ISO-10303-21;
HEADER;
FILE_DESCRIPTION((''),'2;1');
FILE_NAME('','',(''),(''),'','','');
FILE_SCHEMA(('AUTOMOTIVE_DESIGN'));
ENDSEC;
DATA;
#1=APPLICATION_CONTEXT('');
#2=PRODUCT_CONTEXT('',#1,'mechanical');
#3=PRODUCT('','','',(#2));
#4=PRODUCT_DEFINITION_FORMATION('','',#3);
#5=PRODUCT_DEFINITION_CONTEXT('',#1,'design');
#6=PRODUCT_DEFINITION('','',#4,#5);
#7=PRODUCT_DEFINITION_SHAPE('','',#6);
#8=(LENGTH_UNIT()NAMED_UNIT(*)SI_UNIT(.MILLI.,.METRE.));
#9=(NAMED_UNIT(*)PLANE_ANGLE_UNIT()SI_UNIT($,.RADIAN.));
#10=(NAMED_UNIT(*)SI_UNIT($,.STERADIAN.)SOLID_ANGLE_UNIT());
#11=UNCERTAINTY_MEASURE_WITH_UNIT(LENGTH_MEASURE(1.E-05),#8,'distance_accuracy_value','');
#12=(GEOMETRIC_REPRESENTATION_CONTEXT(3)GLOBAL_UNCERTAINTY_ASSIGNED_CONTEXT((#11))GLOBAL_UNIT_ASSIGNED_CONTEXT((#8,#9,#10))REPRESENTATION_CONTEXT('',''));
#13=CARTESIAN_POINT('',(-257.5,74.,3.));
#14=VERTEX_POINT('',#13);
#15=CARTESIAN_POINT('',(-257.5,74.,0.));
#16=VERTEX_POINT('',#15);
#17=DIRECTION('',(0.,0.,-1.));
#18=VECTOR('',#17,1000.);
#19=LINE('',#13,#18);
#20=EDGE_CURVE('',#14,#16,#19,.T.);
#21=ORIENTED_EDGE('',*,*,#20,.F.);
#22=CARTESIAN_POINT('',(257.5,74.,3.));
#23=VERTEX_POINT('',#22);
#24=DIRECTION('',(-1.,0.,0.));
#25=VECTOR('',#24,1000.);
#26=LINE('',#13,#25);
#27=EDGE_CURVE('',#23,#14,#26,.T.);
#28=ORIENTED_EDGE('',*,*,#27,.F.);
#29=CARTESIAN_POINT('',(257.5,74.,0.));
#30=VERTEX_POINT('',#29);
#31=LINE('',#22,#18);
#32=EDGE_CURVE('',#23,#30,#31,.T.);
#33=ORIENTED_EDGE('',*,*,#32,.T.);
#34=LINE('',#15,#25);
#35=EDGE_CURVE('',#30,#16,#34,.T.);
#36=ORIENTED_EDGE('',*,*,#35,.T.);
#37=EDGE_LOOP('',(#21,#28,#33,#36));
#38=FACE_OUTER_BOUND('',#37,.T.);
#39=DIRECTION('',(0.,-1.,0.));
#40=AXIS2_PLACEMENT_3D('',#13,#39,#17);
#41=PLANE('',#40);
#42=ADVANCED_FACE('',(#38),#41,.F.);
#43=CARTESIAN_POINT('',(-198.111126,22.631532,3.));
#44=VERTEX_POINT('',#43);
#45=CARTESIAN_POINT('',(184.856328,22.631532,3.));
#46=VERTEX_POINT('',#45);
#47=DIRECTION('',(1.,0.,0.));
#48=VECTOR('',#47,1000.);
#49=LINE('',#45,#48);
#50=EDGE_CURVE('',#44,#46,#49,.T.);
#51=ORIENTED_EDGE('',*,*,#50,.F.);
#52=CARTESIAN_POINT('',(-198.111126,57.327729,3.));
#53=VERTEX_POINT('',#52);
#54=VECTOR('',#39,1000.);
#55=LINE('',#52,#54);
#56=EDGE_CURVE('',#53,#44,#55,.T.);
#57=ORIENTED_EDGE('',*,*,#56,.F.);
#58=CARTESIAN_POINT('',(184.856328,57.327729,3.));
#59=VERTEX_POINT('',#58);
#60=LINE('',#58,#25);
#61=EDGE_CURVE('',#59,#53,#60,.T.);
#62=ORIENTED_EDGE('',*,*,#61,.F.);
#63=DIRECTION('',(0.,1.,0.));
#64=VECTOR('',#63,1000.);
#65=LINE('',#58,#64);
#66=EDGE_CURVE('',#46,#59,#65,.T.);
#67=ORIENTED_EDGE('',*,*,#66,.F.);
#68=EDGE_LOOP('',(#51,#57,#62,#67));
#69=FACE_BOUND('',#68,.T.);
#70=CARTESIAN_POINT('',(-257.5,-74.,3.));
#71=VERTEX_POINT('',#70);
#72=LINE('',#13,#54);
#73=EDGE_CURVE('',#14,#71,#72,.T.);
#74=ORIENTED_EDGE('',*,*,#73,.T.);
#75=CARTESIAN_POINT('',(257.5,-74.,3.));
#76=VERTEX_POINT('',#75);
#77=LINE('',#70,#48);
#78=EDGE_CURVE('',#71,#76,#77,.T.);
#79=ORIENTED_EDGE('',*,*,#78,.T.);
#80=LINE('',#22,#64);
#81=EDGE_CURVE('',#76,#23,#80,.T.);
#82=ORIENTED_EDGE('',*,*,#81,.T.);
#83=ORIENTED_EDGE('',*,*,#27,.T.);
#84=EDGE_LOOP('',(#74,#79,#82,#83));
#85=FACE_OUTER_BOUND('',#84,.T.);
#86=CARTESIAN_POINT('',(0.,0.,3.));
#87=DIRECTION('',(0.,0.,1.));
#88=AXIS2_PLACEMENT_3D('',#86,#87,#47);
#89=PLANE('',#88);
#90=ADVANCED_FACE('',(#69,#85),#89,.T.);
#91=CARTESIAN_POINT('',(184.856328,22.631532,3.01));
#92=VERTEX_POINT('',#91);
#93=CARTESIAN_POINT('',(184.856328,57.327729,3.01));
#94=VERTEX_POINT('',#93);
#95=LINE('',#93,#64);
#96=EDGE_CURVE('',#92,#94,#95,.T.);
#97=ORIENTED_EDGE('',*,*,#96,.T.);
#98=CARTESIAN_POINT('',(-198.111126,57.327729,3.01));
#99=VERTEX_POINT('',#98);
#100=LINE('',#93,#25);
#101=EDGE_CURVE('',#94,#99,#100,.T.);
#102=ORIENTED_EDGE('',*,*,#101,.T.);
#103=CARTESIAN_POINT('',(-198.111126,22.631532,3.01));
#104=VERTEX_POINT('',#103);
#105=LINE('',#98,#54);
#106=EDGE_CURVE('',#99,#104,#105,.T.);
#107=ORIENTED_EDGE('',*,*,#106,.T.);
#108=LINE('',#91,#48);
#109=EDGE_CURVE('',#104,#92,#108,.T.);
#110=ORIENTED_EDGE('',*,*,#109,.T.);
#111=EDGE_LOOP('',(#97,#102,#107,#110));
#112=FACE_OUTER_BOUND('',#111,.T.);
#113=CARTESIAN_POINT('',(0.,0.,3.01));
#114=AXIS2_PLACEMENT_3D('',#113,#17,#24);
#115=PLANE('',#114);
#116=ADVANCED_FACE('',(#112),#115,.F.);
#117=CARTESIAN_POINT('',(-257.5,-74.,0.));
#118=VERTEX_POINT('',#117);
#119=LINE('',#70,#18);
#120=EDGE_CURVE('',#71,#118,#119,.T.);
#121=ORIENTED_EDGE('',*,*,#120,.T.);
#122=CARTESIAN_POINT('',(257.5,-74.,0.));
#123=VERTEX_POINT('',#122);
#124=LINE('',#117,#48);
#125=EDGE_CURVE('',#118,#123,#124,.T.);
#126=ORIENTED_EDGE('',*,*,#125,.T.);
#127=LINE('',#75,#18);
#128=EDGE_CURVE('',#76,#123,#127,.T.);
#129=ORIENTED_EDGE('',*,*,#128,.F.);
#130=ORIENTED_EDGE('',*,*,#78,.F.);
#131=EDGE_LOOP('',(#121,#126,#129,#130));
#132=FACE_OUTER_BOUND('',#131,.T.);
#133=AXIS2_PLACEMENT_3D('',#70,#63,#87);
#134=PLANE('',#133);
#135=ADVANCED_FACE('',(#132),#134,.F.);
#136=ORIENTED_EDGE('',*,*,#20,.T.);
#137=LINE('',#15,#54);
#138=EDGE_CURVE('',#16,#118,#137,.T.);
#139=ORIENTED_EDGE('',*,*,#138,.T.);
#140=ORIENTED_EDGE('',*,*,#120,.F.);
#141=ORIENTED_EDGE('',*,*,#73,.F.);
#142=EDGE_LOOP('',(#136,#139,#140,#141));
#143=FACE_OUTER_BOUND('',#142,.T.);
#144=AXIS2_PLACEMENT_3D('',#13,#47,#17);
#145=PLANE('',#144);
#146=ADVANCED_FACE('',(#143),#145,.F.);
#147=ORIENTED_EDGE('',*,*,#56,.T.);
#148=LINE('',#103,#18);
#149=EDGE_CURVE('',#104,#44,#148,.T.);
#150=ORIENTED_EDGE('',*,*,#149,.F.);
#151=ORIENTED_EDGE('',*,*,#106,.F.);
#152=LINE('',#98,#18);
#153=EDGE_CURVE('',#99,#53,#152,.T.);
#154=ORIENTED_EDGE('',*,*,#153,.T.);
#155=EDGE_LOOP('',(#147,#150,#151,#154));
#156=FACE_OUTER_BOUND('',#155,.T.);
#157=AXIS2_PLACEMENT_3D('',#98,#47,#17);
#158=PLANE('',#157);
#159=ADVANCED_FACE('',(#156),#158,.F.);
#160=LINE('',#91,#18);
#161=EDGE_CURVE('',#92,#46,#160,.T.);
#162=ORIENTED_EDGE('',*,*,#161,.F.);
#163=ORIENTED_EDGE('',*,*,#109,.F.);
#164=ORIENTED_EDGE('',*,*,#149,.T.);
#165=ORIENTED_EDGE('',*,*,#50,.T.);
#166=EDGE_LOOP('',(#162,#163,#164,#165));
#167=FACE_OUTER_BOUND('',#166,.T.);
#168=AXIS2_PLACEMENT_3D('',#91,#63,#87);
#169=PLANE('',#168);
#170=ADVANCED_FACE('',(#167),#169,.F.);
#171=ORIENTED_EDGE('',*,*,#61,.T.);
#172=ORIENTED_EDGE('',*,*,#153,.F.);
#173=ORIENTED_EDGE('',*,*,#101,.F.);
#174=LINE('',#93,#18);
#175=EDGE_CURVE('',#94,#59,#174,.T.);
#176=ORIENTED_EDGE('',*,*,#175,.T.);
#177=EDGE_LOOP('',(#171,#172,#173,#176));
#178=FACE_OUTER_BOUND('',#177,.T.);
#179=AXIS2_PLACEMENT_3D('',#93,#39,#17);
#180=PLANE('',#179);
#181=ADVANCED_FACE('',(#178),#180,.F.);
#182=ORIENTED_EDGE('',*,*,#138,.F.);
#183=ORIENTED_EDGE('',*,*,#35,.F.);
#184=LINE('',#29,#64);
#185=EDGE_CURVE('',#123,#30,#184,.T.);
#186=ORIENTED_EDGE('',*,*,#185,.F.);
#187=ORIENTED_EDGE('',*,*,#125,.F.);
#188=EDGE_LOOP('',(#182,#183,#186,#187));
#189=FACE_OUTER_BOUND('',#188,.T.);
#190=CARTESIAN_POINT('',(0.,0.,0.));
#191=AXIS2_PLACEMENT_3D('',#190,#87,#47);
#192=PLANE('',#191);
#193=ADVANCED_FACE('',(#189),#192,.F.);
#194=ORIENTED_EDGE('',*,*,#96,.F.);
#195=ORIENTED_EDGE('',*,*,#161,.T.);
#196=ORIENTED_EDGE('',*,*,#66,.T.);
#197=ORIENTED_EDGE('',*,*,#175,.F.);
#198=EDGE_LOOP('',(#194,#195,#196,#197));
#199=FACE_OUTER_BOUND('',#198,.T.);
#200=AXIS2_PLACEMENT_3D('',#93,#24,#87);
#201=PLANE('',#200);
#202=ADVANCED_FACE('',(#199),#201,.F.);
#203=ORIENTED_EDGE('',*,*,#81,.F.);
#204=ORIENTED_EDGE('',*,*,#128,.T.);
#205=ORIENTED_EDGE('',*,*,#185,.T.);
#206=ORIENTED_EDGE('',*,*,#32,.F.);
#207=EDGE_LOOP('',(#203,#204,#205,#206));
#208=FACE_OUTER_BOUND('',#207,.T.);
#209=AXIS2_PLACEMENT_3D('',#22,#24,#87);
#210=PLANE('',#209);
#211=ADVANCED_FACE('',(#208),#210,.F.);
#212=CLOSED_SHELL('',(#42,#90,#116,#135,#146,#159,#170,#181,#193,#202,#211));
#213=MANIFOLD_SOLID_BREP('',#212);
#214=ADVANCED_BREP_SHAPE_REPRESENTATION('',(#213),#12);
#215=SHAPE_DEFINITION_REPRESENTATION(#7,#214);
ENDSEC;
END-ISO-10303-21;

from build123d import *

# Parameters (mm, degrees)
SKETCH1_W           = 515
SKETCH1_H           = 148
BOSS_EXTRUDE1_DEPTH = 3
SKETCH2_W           = 382.967454029
SKETCH2_H           = 34.69619669
BOSS_EXTRUDE2_DEPTH = 0.01


with BuildPart() as part:
    # Sketch1 → Boss-Extrude1 (new body)
    with BuildSketch(Plane.XY):
        Rectangle(SKETCH1_W, SKETCH1_H)
    extrude(amount=BOSS_EXTRUDE1_DEPTH)

    # Sketch2 → Boss-Extrude2 (add)
    with BuildSketch(Plane.XY.offset(3)):
        with Locations((-6.627399213, 39.979630289)):
            Rectangle(SKETCH2_W, SKETCH2_H)
    extrude(amount=BOSS_EXTRUDE2_DEPTH)


solid = part.part
